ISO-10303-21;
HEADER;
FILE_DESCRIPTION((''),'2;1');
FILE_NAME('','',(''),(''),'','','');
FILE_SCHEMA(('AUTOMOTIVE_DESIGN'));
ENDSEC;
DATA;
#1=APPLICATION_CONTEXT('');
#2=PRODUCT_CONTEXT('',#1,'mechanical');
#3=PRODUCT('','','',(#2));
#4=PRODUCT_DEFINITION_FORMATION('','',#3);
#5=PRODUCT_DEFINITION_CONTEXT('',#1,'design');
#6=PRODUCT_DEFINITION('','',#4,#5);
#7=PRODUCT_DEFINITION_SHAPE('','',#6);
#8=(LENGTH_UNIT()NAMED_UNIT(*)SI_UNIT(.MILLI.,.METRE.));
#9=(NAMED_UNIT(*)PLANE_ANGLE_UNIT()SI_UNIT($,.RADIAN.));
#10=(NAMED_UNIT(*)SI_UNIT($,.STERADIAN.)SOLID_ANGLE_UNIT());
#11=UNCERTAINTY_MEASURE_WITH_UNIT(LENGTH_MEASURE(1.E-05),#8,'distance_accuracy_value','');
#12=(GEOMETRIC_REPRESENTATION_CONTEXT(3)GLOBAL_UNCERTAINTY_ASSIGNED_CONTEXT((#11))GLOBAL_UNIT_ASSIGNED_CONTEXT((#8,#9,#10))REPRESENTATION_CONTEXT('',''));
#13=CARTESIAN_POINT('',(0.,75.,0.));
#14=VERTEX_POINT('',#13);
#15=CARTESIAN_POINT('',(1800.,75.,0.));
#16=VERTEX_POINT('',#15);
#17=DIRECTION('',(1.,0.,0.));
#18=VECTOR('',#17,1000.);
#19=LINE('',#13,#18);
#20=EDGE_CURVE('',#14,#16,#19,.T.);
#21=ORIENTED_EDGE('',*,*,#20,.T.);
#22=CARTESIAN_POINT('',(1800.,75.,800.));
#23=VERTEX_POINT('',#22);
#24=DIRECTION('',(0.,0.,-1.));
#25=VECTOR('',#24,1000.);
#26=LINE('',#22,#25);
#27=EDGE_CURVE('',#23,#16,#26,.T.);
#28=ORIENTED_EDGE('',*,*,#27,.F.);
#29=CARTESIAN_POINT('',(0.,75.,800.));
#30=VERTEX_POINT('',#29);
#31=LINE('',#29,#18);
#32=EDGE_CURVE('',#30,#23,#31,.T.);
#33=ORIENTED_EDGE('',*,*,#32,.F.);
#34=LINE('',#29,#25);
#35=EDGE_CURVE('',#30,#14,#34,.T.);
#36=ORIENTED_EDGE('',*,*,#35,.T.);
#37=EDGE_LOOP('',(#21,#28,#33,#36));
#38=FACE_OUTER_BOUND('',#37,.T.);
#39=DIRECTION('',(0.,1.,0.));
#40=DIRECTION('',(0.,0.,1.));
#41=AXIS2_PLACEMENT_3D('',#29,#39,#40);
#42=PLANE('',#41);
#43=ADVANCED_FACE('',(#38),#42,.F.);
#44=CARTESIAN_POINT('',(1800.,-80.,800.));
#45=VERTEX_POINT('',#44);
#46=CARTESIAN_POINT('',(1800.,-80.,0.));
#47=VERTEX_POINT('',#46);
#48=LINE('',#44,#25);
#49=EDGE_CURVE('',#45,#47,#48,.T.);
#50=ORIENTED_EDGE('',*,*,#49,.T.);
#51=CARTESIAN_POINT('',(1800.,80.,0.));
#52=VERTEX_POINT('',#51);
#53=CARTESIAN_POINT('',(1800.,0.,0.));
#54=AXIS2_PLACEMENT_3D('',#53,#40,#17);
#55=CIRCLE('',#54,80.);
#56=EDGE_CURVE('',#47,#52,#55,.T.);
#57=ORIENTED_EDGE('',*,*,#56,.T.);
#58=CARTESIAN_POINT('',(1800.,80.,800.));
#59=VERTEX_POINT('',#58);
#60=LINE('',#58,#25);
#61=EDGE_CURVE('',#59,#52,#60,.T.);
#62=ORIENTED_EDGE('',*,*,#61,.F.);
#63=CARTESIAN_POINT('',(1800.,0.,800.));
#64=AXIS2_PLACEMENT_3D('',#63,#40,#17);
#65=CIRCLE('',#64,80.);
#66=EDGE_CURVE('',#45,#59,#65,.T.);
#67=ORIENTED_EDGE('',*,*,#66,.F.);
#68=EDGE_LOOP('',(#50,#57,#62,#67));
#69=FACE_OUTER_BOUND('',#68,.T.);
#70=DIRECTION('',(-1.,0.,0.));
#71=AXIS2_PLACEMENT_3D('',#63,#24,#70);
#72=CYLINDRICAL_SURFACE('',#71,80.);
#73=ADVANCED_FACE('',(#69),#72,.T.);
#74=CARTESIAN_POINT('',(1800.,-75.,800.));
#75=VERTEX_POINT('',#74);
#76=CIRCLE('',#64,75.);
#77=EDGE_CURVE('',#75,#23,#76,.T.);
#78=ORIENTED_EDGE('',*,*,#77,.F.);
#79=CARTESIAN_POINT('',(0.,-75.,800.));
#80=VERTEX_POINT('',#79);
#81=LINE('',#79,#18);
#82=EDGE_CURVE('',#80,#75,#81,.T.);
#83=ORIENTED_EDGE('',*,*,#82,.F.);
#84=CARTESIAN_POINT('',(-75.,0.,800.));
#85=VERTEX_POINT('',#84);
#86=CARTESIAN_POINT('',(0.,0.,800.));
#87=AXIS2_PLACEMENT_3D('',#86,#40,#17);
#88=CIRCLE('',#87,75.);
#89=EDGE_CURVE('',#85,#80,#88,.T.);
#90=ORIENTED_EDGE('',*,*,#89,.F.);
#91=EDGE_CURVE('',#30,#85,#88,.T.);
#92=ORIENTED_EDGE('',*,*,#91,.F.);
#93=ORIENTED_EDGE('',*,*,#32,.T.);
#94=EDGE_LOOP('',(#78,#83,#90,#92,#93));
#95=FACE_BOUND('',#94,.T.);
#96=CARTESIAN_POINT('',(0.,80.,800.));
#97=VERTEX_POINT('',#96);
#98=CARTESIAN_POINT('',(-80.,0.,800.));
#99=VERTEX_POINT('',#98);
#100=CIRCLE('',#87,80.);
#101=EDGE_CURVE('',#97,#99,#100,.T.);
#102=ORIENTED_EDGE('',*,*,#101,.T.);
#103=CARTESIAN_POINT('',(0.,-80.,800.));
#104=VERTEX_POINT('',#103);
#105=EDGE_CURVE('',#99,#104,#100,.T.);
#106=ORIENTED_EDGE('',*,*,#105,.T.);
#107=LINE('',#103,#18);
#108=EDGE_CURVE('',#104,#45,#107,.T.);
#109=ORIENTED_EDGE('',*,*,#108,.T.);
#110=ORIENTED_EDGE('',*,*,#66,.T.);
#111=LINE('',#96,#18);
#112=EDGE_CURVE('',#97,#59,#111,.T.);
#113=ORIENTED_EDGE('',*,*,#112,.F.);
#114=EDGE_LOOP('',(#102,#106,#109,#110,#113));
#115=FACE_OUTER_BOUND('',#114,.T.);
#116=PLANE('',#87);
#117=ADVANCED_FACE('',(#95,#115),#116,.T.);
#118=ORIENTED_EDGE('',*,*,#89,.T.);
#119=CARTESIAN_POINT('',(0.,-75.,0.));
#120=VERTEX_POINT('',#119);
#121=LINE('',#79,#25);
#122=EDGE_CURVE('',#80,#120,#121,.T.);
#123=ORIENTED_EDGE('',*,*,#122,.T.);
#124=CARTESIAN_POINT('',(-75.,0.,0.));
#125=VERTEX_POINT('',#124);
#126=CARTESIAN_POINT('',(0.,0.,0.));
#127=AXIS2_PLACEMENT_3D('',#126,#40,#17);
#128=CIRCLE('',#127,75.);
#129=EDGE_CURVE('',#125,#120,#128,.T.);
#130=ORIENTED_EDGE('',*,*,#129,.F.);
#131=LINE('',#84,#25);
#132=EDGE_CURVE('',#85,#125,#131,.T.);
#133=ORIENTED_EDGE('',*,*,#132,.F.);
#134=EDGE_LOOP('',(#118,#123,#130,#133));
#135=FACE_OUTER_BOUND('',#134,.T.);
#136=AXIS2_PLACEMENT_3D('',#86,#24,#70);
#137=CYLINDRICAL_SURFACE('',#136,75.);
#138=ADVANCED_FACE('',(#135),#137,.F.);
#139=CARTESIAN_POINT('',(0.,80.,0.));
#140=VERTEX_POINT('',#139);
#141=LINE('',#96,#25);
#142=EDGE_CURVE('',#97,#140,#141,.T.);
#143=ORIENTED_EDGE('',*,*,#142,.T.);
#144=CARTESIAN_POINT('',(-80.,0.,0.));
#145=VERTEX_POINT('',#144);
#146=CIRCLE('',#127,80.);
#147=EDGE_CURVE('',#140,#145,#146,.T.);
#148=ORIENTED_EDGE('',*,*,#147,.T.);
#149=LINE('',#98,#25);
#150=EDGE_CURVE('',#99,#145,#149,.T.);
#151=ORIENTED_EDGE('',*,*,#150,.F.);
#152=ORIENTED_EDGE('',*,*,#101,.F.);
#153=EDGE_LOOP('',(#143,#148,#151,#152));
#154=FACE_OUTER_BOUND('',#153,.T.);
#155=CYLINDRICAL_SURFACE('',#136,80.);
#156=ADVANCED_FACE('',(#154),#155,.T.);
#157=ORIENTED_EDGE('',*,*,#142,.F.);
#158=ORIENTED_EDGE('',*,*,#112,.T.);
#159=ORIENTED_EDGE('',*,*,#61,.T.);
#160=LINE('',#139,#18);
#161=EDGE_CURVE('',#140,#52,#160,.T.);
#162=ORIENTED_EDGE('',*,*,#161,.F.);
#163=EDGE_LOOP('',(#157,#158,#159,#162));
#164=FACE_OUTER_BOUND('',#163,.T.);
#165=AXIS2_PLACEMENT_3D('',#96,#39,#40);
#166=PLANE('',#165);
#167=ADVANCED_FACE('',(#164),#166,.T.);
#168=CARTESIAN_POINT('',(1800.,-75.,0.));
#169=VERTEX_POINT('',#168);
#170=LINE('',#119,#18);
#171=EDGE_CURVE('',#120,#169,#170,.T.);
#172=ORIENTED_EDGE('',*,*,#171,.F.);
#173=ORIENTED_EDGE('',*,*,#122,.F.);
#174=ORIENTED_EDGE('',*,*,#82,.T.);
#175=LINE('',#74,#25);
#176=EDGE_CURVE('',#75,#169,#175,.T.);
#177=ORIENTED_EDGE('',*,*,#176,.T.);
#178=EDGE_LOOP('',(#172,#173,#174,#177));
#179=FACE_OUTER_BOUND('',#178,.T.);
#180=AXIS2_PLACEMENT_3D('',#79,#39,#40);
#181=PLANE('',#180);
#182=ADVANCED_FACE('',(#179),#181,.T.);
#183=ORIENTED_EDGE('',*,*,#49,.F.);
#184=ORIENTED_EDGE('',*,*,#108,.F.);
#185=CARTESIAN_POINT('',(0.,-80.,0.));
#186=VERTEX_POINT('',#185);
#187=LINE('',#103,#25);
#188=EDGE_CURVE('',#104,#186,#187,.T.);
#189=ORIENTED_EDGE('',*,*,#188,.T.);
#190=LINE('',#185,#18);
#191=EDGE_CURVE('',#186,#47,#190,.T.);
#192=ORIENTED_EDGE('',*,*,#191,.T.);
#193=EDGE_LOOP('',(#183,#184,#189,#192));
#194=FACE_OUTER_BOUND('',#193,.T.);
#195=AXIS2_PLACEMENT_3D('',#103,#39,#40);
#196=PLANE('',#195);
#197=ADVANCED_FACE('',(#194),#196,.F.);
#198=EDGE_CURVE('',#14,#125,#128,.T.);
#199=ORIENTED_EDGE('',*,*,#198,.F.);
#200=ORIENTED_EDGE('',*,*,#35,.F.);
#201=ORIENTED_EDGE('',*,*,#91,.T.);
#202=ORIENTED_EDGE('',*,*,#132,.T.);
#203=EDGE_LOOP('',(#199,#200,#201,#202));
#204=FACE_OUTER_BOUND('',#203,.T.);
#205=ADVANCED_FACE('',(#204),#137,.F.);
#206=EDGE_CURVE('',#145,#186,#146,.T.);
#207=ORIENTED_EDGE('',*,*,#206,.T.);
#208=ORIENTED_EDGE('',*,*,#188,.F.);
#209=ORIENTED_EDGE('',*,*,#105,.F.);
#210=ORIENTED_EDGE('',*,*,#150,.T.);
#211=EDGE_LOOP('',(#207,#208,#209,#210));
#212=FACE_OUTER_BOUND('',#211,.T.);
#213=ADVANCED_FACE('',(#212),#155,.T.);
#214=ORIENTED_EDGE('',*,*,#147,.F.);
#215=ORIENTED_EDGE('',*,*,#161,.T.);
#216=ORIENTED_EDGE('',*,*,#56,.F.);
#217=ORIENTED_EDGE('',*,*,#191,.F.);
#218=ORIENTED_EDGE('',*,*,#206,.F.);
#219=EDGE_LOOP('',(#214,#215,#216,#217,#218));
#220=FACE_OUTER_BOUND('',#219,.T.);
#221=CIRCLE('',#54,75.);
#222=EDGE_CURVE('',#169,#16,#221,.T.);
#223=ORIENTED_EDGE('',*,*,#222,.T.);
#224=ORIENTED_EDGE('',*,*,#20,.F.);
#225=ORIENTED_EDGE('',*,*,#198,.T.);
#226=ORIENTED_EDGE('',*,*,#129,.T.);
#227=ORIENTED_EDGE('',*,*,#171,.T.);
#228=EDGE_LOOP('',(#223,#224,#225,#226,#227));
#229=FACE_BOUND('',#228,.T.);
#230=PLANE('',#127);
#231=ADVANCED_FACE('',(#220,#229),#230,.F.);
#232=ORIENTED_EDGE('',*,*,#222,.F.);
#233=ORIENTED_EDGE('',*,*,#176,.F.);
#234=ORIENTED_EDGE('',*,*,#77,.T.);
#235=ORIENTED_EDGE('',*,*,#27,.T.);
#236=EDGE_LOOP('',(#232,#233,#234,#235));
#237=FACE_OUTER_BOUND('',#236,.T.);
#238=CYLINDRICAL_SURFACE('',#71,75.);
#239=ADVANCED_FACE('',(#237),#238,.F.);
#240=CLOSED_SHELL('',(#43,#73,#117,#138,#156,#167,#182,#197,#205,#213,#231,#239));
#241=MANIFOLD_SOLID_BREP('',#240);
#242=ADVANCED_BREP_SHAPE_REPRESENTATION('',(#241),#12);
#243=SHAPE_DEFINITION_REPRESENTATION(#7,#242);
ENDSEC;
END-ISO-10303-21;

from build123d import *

# Parameters (mm, degrees)
EXTRUDE_1_DEPTH = 800


with BuildPart() as part:
    # 草图1 → 拉伸-薄壁1 (new body)
    with BuildSketch(Plane.XY):
        with BuildLine():
            Line((1800, -80), (0, -80))
            ThreePointArc((0, -80), (-80, 0), (0, 80))
            Line((0, 80), (1800, 80))
            ThreePointArc((1800, 80), (1880, 0), (1800, -80))
        make_face()
        with BuildLine():
            Line((1800, -75), (0, -75))
            ThreePointArc((0, -75), (-75, 0), (0, 75))
            Line((0, 75), (1800, 75))
            ThreePointArc((1800, 75), (1875, 0), (1800, -75))
        make_face(mode=Mode.SUBTRACT)
    extrude(amount=EXTRUDE_1_DEPTH)


solid = part.part
